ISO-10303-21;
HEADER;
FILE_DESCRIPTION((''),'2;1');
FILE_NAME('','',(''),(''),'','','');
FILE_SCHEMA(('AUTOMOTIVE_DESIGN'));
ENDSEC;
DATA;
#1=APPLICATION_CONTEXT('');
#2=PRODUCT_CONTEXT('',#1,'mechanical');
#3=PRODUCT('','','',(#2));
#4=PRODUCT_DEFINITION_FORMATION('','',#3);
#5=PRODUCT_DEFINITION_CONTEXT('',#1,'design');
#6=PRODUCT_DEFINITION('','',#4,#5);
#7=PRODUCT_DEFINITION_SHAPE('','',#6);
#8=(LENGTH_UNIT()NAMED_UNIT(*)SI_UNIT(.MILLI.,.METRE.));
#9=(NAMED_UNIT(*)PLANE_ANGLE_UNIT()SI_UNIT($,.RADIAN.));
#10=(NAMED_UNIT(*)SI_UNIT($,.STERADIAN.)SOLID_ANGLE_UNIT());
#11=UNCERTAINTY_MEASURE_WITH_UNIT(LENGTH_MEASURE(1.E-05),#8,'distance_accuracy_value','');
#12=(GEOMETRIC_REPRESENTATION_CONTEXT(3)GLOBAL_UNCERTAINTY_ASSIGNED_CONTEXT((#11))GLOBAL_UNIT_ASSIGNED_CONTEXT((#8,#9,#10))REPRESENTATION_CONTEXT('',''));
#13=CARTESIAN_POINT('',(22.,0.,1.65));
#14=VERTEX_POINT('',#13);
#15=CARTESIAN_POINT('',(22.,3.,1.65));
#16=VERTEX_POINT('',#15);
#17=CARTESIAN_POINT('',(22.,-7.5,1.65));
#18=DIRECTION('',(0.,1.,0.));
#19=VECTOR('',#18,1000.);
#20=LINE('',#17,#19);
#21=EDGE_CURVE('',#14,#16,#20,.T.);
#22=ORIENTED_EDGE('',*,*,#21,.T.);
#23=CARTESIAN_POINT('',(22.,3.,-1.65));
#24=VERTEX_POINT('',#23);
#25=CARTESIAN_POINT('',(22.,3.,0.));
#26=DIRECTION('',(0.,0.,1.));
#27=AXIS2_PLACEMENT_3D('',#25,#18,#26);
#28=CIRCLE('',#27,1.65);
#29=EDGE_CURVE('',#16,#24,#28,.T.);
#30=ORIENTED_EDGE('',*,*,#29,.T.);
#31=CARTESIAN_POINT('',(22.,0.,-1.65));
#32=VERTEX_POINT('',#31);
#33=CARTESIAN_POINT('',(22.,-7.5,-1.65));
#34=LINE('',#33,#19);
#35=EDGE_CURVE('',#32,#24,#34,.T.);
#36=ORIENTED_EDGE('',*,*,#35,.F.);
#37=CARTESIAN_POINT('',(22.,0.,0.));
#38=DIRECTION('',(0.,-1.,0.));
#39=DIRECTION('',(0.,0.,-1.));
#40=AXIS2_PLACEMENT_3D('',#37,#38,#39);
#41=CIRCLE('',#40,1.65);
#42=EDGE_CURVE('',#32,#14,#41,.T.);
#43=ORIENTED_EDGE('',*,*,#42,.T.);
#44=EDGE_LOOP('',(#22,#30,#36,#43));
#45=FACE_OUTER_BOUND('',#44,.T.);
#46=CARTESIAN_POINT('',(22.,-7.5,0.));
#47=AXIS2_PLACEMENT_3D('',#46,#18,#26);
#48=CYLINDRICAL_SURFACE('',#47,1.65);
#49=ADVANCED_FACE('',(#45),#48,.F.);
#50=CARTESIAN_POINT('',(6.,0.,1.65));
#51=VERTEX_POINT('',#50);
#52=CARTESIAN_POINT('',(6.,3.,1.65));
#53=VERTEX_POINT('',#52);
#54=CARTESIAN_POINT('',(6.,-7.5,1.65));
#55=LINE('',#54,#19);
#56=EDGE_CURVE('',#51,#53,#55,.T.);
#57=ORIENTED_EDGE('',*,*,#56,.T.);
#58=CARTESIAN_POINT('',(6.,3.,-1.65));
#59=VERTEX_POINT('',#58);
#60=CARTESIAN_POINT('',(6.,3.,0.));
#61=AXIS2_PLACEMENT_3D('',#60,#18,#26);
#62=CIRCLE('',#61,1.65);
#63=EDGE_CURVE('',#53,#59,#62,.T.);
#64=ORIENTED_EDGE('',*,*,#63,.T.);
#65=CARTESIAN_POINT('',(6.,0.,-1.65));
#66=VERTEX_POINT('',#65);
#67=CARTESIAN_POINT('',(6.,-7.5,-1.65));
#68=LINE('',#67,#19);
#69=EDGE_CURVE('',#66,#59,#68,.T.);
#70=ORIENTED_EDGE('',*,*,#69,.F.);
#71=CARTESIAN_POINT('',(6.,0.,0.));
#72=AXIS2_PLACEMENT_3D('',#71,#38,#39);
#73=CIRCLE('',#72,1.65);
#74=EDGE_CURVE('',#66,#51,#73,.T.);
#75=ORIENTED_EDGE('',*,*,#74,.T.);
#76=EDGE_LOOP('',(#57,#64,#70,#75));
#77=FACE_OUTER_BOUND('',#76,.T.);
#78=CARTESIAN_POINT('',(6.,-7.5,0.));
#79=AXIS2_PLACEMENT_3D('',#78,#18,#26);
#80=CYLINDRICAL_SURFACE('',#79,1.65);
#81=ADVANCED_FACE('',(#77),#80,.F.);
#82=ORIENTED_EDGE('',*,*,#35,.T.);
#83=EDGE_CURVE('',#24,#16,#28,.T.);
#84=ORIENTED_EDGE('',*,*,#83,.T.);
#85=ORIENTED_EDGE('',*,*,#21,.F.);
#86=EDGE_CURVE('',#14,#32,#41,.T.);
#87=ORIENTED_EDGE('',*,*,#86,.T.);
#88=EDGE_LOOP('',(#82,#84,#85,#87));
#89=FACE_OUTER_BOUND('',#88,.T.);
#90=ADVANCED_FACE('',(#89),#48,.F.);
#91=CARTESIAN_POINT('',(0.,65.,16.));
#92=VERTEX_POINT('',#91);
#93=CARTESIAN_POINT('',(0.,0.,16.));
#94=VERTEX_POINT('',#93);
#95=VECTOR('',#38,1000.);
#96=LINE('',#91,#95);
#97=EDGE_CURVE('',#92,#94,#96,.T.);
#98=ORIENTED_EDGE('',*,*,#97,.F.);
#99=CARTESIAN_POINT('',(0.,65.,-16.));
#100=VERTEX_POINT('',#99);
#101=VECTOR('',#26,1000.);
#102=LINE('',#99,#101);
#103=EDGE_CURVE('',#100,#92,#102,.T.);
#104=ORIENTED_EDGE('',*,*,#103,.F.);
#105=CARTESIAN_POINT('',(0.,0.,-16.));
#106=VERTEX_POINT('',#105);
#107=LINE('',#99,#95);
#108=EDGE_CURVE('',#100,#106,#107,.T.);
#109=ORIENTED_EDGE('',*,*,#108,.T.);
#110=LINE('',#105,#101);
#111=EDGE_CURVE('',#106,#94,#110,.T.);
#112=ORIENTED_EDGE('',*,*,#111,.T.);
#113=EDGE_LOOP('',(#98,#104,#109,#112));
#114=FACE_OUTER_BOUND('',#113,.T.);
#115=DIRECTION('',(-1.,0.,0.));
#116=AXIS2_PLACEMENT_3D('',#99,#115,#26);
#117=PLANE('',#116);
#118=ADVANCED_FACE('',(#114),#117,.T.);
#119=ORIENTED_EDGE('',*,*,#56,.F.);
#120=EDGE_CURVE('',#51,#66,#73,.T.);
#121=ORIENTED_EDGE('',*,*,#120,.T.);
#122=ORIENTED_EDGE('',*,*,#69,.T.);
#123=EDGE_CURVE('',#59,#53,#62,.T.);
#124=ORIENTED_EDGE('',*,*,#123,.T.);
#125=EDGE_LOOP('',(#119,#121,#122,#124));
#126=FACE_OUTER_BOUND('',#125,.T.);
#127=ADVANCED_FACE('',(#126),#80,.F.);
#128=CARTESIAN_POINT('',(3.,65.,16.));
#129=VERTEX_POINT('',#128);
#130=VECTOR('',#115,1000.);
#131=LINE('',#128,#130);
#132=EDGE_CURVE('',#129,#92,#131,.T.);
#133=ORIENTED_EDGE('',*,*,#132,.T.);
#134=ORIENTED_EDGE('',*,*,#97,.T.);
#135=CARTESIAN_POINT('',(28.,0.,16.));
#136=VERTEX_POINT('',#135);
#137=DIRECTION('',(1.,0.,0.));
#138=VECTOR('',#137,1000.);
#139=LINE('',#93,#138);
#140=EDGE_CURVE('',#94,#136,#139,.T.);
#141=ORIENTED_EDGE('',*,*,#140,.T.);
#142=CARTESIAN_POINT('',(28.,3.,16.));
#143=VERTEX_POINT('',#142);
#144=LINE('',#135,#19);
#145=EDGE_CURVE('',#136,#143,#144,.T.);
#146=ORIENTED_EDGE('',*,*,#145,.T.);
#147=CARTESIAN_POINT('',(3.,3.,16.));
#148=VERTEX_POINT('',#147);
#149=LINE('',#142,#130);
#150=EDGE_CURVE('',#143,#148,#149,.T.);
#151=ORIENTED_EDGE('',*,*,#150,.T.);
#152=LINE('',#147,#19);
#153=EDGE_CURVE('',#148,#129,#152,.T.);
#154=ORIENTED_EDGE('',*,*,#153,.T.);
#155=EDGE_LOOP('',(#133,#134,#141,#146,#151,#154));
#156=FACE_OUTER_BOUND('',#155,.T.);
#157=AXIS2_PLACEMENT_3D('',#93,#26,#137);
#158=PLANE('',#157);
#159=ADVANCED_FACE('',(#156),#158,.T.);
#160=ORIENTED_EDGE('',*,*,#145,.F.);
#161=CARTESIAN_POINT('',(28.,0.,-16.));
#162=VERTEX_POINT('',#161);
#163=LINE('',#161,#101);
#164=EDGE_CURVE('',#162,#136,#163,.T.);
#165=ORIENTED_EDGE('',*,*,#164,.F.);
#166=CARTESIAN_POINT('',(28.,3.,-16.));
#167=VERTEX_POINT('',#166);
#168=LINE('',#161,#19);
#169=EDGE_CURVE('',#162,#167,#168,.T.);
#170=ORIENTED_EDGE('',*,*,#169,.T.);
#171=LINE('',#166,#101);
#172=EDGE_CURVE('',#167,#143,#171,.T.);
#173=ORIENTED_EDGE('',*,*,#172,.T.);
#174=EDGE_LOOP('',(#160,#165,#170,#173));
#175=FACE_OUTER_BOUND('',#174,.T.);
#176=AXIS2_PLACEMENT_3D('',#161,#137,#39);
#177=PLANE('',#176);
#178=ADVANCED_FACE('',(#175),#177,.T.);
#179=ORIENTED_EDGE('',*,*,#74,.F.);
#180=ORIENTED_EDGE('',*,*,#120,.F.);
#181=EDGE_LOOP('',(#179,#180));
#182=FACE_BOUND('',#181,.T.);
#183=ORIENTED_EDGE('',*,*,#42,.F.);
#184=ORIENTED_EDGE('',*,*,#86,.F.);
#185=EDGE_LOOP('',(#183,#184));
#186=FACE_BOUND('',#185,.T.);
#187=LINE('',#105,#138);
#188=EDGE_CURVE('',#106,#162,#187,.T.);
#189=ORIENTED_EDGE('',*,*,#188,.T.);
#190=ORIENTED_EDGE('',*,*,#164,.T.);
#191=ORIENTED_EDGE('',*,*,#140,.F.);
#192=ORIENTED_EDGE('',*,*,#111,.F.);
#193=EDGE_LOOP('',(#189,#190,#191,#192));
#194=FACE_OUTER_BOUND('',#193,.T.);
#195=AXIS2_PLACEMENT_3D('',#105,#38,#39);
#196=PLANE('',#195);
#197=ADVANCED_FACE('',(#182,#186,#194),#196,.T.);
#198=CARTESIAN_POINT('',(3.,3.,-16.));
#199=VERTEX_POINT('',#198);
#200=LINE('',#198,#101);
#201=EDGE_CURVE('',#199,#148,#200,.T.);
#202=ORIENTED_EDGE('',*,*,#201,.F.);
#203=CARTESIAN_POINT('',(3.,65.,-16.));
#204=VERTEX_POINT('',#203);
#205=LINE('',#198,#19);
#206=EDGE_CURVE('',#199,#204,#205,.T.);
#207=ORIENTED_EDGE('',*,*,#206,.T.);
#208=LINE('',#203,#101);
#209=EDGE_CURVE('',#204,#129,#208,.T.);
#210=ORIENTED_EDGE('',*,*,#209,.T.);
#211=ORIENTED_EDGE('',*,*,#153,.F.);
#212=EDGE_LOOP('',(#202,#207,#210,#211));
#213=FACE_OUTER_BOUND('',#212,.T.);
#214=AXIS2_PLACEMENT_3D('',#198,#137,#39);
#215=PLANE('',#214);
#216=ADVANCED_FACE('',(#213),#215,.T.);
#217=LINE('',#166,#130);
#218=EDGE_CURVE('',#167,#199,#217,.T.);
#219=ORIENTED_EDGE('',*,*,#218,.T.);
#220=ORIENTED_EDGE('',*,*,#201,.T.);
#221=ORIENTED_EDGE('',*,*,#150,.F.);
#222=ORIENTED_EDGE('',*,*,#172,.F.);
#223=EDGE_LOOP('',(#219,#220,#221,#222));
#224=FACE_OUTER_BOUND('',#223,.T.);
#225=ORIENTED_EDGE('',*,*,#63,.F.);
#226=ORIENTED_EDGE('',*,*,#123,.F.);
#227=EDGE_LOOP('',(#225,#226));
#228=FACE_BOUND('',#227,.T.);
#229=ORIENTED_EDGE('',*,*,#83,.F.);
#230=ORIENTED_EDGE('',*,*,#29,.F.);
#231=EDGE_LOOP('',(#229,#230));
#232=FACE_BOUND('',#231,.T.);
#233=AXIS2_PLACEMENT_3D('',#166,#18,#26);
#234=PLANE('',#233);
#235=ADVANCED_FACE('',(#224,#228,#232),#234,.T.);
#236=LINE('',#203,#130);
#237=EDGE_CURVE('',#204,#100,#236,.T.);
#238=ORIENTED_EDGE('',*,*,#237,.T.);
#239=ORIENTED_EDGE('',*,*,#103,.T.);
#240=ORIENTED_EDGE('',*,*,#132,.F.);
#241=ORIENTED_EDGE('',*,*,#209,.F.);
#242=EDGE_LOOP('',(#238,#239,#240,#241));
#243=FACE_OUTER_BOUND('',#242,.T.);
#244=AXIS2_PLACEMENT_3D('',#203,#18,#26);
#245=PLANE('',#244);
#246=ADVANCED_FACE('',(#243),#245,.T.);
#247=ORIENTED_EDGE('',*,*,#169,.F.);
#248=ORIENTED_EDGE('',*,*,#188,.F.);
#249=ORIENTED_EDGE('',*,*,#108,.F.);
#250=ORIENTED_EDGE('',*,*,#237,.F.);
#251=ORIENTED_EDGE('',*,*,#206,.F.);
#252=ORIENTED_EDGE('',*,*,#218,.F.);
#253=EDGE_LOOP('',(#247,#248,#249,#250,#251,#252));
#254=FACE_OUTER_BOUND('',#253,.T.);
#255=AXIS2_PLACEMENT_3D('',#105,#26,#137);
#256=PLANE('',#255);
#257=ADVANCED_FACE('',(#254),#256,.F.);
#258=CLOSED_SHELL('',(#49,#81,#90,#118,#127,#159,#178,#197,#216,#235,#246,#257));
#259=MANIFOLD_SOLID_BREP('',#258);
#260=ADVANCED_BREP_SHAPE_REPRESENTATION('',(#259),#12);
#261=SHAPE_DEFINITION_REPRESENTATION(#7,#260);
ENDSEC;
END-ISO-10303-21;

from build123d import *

# Parameters (mm, degrees)
EXTRUDE_1_DEPTH     = 16
SKETCH_2_R          = 1.65
CUT_EXTRUDE_1_DEPTH = 7.5


with BuildPart() as part:
    # 草图1 → 凸台-拉伸1 (new, symmetric)
    with BuildSketch(Plane.XY):
        Polygon((0, 0), (28, 0), (28, 3), (3, 3), (3, 65), (0, 65), align=None)
    extrude(amount=EXTRUDE_1_DEPTH, both=True)

    # 草图2 → 切除-拉伸1 (cut, symmetric)
    with BuildSketch(Plane(origin=(0, 0, 0), x_dir=(1, 0, 0), z_dir=(0, 1, 0))):
        with Locations(Location((6, 0, 0), (0, 0, 270))):
            Circle(SKETCH_2_R)
        with Locations(Location((22, 0, 0), (0, 0, 270))):
            Circle(SKETCH_2_R)
    extrude(amount=CUT_EXTRUDE_1_DEPTH, both=True, mode=Mode.SUBTRACT)


solid = part.part
